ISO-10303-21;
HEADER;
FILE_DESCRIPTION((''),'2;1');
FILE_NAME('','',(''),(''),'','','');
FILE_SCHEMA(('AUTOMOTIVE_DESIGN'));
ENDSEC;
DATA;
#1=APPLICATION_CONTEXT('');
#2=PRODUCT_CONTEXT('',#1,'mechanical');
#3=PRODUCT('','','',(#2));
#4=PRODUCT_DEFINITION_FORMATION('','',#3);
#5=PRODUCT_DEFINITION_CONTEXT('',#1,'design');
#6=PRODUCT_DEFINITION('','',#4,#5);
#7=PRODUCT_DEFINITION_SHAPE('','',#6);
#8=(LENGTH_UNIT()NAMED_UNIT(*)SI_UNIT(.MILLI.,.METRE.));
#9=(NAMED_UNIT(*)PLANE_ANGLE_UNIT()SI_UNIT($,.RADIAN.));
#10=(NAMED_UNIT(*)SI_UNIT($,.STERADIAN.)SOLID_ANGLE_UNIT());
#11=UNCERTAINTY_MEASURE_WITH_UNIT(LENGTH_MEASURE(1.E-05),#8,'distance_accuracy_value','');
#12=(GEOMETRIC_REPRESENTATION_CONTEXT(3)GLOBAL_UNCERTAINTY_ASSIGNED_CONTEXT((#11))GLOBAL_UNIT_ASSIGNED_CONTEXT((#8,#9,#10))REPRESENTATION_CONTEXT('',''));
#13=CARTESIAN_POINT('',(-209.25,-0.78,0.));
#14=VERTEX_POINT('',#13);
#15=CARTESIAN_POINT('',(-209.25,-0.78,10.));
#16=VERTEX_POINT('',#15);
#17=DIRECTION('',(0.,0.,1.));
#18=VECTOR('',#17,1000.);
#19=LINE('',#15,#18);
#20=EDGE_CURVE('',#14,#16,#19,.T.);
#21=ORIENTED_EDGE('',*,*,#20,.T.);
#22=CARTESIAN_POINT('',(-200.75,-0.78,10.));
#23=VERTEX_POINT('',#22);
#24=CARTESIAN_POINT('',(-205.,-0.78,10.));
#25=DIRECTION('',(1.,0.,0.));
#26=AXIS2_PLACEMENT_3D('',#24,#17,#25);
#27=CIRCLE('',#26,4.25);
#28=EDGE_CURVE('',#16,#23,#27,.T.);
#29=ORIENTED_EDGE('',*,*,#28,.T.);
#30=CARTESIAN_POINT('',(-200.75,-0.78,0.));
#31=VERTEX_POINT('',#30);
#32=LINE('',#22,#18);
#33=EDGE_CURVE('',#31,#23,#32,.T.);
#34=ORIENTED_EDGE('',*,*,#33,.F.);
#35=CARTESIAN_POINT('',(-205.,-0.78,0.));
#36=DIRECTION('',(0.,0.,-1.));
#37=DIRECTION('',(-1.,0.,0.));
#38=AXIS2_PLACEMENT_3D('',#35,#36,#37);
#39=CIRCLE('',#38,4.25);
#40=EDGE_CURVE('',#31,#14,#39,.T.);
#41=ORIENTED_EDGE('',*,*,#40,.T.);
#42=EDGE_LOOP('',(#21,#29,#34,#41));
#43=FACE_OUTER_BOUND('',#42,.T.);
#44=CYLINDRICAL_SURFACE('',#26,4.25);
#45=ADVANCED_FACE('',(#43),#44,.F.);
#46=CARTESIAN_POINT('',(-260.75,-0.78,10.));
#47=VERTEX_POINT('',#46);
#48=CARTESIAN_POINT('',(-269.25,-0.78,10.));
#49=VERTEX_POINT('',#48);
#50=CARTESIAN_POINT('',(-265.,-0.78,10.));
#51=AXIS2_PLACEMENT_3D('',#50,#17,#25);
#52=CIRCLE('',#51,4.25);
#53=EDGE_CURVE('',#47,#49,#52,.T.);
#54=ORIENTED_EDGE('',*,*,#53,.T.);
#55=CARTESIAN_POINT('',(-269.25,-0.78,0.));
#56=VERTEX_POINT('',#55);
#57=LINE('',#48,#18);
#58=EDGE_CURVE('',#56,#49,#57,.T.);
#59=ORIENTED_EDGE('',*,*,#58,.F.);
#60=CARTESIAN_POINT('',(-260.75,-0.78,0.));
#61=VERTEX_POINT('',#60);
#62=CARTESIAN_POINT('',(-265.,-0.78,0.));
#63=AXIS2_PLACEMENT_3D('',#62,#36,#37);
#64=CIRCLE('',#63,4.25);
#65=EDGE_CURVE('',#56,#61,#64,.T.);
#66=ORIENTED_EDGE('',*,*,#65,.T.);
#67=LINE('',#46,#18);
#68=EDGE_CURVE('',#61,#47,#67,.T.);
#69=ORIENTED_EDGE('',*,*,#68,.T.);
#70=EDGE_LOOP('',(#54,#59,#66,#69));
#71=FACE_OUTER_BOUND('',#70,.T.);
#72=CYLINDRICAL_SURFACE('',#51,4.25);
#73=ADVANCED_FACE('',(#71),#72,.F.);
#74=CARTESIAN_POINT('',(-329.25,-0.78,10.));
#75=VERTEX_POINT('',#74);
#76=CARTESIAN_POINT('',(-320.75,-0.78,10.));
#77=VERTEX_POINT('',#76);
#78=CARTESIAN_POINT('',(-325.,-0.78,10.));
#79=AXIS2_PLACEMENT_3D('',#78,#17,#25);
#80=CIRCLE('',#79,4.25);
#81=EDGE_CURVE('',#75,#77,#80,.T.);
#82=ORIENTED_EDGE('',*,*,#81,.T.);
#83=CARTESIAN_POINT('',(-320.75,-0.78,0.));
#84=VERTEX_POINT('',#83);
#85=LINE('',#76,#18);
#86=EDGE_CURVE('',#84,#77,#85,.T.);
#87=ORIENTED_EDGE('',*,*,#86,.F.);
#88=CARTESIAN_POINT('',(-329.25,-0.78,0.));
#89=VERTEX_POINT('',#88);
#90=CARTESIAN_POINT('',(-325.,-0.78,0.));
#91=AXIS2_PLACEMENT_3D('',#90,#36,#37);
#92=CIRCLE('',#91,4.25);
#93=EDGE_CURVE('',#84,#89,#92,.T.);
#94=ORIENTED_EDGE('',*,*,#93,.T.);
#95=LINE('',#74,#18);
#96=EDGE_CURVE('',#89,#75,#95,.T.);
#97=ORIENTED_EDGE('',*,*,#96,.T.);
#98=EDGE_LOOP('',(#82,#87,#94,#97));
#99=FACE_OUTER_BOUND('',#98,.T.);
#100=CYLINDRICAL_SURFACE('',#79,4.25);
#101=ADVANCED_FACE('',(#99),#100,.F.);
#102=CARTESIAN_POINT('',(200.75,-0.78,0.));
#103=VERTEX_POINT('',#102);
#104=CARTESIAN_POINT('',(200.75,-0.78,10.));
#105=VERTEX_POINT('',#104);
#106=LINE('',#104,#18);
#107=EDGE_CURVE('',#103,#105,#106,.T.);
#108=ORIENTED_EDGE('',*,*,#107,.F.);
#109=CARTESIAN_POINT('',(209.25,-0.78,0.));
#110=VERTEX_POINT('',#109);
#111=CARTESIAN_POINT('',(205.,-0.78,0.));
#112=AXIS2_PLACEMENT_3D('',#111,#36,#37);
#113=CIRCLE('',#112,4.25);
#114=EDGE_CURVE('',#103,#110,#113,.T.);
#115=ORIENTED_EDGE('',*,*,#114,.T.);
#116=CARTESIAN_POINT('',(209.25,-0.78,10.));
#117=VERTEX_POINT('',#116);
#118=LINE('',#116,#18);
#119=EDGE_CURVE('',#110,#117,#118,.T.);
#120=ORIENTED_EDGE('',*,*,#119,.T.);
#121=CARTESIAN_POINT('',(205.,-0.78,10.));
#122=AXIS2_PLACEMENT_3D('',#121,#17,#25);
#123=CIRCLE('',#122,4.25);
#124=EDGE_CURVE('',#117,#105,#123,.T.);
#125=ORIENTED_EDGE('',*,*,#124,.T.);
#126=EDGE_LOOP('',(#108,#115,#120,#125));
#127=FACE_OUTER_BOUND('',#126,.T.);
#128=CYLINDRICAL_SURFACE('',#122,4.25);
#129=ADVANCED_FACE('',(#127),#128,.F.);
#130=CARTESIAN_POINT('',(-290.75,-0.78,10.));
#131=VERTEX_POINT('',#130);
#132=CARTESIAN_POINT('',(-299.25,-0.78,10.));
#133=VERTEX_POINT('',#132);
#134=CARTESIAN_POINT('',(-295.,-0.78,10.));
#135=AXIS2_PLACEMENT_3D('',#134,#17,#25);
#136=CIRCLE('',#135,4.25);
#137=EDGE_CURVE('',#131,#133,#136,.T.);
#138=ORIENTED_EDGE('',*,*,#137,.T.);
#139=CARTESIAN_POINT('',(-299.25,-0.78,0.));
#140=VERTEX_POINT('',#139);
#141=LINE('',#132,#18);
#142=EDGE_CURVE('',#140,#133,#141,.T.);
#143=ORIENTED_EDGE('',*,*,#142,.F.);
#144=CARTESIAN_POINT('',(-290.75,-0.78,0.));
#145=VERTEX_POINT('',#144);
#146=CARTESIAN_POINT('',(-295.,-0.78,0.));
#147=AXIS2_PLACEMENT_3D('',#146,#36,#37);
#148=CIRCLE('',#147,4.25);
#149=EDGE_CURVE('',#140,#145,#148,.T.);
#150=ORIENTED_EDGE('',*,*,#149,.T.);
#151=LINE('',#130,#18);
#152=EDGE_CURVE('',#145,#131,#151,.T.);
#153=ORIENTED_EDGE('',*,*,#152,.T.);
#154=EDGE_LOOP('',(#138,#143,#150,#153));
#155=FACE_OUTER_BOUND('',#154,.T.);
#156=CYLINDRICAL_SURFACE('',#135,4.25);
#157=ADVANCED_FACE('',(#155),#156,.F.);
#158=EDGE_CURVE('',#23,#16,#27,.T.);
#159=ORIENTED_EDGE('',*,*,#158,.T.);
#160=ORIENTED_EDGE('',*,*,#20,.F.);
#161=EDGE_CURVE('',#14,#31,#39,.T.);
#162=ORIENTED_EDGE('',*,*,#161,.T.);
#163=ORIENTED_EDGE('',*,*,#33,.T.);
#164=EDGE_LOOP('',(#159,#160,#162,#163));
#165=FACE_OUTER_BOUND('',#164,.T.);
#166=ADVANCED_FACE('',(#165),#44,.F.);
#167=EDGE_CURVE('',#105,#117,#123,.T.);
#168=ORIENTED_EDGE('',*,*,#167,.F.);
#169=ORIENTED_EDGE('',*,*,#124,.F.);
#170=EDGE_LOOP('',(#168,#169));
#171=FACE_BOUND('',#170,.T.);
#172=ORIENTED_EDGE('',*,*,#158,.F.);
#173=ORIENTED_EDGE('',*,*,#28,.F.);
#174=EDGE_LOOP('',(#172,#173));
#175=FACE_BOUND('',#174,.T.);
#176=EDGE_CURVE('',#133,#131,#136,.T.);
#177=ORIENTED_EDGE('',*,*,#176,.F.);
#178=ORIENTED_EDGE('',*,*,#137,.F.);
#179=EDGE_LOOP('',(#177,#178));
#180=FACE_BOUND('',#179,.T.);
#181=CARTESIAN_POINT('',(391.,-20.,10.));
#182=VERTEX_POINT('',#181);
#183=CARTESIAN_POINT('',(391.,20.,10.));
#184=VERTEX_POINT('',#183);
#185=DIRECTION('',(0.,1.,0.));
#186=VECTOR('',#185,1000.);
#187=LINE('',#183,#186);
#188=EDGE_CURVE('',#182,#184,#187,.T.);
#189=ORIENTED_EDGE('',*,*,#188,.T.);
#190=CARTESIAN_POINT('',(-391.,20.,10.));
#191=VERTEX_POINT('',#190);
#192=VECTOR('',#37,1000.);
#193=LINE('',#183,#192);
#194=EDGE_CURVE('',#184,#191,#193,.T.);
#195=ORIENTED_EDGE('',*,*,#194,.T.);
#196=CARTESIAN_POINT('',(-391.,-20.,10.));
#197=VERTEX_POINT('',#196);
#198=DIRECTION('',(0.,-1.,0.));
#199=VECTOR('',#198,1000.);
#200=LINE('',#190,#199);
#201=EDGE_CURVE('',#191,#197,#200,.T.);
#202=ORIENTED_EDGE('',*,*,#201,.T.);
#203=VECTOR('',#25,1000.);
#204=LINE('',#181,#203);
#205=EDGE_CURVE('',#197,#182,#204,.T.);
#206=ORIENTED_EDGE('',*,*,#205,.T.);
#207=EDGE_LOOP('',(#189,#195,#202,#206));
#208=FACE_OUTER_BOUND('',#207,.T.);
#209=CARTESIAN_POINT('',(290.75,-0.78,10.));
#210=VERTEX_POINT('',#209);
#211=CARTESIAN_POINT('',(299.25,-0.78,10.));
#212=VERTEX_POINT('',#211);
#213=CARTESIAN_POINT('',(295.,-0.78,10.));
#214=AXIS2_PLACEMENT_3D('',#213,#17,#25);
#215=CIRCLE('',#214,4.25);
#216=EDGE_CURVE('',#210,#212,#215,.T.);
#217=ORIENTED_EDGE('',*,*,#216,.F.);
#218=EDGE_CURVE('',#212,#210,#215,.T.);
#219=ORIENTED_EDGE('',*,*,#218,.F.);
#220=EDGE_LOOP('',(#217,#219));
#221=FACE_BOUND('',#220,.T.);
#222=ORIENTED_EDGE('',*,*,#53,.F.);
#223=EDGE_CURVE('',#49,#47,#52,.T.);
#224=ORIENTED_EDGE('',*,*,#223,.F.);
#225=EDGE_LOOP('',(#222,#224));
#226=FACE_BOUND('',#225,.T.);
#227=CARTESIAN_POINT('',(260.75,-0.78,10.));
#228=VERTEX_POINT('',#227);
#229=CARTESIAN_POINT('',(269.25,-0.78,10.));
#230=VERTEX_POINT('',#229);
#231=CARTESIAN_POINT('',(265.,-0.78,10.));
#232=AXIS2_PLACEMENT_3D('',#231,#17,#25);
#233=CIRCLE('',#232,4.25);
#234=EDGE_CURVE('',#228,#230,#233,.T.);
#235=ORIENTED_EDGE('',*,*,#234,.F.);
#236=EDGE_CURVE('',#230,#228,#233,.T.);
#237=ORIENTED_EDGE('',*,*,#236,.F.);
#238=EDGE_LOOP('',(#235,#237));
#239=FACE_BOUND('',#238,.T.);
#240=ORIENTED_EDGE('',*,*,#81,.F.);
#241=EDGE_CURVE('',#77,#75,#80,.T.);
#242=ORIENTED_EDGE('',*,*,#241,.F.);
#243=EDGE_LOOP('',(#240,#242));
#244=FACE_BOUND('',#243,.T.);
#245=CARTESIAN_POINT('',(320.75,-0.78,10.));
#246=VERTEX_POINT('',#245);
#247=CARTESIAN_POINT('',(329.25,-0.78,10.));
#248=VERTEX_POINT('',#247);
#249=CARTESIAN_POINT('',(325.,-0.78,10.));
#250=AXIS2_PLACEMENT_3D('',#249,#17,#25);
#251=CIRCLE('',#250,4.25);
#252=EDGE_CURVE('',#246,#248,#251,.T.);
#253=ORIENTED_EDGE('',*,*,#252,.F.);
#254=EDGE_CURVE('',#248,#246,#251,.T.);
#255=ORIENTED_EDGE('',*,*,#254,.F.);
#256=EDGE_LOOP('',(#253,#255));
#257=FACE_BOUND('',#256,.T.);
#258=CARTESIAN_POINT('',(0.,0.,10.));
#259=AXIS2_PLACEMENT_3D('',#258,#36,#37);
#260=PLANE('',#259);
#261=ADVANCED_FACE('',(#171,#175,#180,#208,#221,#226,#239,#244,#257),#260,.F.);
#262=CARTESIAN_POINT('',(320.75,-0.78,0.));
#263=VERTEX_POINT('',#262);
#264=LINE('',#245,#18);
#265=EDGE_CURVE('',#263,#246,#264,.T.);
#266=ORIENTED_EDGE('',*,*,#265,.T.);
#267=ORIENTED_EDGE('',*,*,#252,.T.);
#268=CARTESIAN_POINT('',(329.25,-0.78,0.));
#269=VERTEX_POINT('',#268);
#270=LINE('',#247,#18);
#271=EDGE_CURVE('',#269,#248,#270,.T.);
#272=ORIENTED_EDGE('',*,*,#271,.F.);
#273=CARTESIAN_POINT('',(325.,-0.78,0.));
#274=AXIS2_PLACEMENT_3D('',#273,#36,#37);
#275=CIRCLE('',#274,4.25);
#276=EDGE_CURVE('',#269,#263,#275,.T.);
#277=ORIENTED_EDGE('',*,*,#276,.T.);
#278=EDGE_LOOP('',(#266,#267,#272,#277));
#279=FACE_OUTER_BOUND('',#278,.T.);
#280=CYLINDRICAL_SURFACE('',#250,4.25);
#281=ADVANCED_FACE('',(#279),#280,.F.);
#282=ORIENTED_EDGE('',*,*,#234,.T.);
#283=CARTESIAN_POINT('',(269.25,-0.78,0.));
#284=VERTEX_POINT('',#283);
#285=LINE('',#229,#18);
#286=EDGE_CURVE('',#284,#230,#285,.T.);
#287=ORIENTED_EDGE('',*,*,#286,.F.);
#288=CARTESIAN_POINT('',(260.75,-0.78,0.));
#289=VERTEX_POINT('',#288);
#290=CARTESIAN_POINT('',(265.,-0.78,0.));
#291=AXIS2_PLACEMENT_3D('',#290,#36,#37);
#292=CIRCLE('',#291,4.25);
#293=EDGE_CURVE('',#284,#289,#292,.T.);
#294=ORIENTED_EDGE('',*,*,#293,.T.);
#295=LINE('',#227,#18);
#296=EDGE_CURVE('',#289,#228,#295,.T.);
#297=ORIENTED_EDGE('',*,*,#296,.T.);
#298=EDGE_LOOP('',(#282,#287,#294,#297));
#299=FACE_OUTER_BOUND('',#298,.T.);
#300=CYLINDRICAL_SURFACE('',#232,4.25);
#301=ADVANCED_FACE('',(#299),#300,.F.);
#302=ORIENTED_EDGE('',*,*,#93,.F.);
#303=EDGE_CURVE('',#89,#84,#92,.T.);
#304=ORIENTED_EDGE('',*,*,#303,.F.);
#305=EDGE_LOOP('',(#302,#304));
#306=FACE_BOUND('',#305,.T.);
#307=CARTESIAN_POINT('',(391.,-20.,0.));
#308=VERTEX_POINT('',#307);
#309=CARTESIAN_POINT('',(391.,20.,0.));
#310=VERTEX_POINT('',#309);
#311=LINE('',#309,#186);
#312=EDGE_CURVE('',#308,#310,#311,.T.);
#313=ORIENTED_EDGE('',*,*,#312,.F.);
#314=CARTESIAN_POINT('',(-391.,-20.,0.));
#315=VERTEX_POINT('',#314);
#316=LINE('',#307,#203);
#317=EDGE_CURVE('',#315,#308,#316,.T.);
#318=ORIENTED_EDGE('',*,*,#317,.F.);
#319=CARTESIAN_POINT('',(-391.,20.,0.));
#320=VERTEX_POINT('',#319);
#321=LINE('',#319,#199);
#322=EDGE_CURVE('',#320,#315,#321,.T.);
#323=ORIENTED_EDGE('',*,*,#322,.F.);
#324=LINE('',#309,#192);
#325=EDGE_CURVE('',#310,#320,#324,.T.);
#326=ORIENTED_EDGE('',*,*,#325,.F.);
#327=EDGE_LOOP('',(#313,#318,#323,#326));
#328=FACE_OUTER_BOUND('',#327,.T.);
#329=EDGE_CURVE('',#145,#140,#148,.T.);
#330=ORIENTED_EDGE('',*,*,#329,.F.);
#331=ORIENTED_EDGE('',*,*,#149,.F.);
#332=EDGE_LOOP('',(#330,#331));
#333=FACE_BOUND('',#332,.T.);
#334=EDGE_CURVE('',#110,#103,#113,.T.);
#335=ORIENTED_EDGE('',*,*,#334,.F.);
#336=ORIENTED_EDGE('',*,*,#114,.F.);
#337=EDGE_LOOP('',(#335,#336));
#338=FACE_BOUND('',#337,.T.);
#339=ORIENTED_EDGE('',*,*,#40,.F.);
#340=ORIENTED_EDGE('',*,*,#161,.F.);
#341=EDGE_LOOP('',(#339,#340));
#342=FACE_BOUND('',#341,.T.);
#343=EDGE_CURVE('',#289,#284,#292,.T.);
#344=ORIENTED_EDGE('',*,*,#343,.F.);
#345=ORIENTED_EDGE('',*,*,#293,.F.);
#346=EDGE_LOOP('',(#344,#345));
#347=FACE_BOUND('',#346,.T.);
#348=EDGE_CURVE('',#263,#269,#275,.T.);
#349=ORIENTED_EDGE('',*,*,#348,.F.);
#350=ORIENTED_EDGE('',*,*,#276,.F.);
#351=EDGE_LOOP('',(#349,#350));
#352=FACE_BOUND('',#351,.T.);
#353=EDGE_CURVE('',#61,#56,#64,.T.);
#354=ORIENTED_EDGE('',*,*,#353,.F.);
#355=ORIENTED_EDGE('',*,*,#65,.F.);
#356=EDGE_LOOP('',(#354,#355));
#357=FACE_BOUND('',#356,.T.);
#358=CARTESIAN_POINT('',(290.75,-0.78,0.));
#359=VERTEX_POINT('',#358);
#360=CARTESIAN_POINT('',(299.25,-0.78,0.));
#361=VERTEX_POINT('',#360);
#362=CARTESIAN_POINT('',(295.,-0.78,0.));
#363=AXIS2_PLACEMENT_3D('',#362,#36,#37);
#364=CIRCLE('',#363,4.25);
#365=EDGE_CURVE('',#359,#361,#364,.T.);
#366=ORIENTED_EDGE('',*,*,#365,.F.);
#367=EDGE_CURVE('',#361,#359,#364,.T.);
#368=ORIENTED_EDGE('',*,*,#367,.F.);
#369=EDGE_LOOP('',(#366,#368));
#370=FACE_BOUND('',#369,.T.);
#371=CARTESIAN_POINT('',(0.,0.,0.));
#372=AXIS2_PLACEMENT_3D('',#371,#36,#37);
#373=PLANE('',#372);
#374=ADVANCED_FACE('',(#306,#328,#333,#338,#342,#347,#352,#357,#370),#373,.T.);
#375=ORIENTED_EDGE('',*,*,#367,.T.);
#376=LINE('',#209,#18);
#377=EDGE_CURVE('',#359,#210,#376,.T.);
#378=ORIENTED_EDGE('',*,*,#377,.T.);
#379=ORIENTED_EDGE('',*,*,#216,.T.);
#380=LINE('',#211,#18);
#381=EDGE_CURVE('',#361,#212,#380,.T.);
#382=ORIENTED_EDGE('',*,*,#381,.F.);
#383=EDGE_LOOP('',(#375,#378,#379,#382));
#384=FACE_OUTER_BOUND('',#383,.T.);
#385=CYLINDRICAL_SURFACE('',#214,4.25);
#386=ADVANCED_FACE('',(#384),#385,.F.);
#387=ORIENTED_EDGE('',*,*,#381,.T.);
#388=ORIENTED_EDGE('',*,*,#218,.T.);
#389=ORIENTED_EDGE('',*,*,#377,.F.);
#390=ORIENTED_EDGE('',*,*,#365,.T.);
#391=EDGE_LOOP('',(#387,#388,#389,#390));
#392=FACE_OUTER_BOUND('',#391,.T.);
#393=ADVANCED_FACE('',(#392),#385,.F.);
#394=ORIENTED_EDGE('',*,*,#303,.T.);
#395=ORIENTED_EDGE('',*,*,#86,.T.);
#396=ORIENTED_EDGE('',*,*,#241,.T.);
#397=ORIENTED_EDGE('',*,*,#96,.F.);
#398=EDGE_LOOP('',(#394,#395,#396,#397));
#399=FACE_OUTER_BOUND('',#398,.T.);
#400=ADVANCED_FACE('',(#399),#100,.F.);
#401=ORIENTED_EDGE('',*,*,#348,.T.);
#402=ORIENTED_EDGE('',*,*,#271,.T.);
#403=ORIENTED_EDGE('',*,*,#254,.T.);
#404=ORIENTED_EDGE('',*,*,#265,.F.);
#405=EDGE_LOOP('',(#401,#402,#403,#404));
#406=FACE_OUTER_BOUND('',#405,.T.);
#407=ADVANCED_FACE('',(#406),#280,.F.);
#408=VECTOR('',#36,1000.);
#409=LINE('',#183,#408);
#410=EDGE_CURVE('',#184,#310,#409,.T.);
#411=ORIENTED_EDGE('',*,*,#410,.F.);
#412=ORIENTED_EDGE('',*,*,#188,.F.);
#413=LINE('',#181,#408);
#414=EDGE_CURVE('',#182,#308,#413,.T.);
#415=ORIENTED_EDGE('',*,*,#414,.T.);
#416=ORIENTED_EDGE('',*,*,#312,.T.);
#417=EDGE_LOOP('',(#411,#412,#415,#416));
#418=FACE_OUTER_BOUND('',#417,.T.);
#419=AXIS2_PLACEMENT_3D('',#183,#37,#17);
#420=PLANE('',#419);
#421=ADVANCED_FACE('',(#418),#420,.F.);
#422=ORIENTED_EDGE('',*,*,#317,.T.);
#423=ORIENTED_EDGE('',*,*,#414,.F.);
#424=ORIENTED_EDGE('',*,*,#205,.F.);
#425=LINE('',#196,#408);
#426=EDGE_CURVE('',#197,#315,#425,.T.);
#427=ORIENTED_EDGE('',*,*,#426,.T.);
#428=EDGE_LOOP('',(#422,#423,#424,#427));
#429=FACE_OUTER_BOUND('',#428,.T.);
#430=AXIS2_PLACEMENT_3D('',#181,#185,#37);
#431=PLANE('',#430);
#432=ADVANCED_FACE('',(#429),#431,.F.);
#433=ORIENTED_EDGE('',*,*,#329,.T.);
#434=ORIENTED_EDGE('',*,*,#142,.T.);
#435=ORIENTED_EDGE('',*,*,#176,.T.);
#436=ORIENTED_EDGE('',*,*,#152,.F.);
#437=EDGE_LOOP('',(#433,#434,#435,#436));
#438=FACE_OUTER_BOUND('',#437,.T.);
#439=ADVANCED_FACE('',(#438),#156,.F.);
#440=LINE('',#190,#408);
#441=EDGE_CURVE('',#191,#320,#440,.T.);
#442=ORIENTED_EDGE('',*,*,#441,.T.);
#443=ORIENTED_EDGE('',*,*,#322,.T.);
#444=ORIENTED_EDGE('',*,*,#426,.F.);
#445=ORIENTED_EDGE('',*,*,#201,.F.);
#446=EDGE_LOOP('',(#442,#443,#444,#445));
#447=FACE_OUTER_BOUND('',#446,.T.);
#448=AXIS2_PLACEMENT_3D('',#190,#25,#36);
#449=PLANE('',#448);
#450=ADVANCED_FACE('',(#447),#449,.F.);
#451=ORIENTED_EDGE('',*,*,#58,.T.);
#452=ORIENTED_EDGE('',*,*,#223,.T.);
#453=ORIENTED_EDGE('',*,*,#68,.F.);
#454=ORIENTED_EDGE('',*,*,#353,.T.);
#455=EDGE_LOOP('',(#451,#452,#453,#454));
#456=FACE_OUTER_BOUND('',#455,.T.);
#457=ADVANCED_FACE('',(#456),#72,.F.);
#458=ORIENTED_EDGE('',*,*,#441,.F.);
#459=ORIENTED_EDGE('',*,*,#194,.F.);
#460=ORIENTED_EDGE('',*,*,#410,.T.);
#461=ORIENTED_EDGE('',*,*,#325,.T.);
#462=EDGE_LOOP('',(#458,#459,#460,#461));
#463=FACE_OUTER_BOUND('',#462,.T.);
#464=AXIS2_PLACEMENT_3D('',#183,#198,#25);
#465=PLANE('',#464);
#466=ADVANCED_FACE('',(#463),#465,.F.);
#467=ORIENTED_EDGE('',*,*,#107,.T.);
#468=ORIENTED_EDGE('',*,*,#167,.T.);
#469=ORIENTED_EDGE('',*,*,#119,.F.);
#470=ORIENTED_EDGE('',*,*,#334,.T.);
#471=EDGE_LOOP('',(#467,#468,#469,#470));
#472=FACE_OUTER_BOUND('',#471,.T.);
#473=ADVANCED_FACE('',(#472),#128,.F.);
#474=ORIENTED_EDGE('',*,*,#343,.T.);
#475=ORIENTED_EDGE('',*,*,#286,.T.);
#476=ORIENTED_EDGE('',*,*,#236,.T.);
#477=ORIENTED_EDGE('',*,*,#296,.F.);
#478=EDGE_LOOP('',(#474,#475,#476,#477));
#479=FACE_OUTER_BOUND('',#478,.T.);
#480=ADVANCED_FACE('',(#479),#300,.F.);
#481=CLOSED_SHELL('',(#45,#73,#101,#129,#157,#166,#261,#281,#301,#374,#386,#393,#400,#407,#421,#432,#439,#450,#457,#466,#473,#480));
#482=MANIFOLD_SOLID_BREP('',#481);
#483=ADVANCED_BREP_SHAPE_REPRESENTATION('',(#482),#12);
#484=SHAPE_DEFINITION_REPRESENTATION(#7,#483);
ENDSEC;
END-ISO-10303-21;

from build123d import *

# Parameters (mm, degrees)
SKETCH1_W              = 782
SKETCH1_H              = 40
BOSS_EXTRUDE1_DEPTH    = 10
M10_TAPPED_HOLE3_D     = 8.5
M10_TAPPED_HOLE3_DEPTH = 24.5
M10_TAPPED_HOLE3_TIP   = 2.553657631


with BuildPart() as part:
    # Sketch1 → Boss-Extrude1 (new body)
    with BuildSketch(Plane.XY):
        Rectangle(SKETCH1_W, SKETCH1_H)
    extrude(amount=BOSS_EXTRUDE1_DEPTH)

    # M10 Tapped Hole3
    with Locations(Plane.XY.offset(10)):
        with Locations((-325, -0.78), (-295, -0.78), (-265, -0.78), (-205, -0.78), (205, -0.78), (265, -0.78), (295, -0.78), (325, -0.78)):
            Hole(M10_TAPPED_HOLE3_D / 2, depth=M10_TAPPED_HOLE3_DEPTH)
            with Locations((0, 0, -(M10_TAPPED_HOLE3_DEPTH + M10_TAPPED_HOLE3_TIP / 2))):  # 118° drill point
                Cone(0, M10_TAPPED_HOLE3_D / 2, M10_TAPPED_HOLE3_TIP, mode=Mode.SUBTRACT)


solid = part.part
